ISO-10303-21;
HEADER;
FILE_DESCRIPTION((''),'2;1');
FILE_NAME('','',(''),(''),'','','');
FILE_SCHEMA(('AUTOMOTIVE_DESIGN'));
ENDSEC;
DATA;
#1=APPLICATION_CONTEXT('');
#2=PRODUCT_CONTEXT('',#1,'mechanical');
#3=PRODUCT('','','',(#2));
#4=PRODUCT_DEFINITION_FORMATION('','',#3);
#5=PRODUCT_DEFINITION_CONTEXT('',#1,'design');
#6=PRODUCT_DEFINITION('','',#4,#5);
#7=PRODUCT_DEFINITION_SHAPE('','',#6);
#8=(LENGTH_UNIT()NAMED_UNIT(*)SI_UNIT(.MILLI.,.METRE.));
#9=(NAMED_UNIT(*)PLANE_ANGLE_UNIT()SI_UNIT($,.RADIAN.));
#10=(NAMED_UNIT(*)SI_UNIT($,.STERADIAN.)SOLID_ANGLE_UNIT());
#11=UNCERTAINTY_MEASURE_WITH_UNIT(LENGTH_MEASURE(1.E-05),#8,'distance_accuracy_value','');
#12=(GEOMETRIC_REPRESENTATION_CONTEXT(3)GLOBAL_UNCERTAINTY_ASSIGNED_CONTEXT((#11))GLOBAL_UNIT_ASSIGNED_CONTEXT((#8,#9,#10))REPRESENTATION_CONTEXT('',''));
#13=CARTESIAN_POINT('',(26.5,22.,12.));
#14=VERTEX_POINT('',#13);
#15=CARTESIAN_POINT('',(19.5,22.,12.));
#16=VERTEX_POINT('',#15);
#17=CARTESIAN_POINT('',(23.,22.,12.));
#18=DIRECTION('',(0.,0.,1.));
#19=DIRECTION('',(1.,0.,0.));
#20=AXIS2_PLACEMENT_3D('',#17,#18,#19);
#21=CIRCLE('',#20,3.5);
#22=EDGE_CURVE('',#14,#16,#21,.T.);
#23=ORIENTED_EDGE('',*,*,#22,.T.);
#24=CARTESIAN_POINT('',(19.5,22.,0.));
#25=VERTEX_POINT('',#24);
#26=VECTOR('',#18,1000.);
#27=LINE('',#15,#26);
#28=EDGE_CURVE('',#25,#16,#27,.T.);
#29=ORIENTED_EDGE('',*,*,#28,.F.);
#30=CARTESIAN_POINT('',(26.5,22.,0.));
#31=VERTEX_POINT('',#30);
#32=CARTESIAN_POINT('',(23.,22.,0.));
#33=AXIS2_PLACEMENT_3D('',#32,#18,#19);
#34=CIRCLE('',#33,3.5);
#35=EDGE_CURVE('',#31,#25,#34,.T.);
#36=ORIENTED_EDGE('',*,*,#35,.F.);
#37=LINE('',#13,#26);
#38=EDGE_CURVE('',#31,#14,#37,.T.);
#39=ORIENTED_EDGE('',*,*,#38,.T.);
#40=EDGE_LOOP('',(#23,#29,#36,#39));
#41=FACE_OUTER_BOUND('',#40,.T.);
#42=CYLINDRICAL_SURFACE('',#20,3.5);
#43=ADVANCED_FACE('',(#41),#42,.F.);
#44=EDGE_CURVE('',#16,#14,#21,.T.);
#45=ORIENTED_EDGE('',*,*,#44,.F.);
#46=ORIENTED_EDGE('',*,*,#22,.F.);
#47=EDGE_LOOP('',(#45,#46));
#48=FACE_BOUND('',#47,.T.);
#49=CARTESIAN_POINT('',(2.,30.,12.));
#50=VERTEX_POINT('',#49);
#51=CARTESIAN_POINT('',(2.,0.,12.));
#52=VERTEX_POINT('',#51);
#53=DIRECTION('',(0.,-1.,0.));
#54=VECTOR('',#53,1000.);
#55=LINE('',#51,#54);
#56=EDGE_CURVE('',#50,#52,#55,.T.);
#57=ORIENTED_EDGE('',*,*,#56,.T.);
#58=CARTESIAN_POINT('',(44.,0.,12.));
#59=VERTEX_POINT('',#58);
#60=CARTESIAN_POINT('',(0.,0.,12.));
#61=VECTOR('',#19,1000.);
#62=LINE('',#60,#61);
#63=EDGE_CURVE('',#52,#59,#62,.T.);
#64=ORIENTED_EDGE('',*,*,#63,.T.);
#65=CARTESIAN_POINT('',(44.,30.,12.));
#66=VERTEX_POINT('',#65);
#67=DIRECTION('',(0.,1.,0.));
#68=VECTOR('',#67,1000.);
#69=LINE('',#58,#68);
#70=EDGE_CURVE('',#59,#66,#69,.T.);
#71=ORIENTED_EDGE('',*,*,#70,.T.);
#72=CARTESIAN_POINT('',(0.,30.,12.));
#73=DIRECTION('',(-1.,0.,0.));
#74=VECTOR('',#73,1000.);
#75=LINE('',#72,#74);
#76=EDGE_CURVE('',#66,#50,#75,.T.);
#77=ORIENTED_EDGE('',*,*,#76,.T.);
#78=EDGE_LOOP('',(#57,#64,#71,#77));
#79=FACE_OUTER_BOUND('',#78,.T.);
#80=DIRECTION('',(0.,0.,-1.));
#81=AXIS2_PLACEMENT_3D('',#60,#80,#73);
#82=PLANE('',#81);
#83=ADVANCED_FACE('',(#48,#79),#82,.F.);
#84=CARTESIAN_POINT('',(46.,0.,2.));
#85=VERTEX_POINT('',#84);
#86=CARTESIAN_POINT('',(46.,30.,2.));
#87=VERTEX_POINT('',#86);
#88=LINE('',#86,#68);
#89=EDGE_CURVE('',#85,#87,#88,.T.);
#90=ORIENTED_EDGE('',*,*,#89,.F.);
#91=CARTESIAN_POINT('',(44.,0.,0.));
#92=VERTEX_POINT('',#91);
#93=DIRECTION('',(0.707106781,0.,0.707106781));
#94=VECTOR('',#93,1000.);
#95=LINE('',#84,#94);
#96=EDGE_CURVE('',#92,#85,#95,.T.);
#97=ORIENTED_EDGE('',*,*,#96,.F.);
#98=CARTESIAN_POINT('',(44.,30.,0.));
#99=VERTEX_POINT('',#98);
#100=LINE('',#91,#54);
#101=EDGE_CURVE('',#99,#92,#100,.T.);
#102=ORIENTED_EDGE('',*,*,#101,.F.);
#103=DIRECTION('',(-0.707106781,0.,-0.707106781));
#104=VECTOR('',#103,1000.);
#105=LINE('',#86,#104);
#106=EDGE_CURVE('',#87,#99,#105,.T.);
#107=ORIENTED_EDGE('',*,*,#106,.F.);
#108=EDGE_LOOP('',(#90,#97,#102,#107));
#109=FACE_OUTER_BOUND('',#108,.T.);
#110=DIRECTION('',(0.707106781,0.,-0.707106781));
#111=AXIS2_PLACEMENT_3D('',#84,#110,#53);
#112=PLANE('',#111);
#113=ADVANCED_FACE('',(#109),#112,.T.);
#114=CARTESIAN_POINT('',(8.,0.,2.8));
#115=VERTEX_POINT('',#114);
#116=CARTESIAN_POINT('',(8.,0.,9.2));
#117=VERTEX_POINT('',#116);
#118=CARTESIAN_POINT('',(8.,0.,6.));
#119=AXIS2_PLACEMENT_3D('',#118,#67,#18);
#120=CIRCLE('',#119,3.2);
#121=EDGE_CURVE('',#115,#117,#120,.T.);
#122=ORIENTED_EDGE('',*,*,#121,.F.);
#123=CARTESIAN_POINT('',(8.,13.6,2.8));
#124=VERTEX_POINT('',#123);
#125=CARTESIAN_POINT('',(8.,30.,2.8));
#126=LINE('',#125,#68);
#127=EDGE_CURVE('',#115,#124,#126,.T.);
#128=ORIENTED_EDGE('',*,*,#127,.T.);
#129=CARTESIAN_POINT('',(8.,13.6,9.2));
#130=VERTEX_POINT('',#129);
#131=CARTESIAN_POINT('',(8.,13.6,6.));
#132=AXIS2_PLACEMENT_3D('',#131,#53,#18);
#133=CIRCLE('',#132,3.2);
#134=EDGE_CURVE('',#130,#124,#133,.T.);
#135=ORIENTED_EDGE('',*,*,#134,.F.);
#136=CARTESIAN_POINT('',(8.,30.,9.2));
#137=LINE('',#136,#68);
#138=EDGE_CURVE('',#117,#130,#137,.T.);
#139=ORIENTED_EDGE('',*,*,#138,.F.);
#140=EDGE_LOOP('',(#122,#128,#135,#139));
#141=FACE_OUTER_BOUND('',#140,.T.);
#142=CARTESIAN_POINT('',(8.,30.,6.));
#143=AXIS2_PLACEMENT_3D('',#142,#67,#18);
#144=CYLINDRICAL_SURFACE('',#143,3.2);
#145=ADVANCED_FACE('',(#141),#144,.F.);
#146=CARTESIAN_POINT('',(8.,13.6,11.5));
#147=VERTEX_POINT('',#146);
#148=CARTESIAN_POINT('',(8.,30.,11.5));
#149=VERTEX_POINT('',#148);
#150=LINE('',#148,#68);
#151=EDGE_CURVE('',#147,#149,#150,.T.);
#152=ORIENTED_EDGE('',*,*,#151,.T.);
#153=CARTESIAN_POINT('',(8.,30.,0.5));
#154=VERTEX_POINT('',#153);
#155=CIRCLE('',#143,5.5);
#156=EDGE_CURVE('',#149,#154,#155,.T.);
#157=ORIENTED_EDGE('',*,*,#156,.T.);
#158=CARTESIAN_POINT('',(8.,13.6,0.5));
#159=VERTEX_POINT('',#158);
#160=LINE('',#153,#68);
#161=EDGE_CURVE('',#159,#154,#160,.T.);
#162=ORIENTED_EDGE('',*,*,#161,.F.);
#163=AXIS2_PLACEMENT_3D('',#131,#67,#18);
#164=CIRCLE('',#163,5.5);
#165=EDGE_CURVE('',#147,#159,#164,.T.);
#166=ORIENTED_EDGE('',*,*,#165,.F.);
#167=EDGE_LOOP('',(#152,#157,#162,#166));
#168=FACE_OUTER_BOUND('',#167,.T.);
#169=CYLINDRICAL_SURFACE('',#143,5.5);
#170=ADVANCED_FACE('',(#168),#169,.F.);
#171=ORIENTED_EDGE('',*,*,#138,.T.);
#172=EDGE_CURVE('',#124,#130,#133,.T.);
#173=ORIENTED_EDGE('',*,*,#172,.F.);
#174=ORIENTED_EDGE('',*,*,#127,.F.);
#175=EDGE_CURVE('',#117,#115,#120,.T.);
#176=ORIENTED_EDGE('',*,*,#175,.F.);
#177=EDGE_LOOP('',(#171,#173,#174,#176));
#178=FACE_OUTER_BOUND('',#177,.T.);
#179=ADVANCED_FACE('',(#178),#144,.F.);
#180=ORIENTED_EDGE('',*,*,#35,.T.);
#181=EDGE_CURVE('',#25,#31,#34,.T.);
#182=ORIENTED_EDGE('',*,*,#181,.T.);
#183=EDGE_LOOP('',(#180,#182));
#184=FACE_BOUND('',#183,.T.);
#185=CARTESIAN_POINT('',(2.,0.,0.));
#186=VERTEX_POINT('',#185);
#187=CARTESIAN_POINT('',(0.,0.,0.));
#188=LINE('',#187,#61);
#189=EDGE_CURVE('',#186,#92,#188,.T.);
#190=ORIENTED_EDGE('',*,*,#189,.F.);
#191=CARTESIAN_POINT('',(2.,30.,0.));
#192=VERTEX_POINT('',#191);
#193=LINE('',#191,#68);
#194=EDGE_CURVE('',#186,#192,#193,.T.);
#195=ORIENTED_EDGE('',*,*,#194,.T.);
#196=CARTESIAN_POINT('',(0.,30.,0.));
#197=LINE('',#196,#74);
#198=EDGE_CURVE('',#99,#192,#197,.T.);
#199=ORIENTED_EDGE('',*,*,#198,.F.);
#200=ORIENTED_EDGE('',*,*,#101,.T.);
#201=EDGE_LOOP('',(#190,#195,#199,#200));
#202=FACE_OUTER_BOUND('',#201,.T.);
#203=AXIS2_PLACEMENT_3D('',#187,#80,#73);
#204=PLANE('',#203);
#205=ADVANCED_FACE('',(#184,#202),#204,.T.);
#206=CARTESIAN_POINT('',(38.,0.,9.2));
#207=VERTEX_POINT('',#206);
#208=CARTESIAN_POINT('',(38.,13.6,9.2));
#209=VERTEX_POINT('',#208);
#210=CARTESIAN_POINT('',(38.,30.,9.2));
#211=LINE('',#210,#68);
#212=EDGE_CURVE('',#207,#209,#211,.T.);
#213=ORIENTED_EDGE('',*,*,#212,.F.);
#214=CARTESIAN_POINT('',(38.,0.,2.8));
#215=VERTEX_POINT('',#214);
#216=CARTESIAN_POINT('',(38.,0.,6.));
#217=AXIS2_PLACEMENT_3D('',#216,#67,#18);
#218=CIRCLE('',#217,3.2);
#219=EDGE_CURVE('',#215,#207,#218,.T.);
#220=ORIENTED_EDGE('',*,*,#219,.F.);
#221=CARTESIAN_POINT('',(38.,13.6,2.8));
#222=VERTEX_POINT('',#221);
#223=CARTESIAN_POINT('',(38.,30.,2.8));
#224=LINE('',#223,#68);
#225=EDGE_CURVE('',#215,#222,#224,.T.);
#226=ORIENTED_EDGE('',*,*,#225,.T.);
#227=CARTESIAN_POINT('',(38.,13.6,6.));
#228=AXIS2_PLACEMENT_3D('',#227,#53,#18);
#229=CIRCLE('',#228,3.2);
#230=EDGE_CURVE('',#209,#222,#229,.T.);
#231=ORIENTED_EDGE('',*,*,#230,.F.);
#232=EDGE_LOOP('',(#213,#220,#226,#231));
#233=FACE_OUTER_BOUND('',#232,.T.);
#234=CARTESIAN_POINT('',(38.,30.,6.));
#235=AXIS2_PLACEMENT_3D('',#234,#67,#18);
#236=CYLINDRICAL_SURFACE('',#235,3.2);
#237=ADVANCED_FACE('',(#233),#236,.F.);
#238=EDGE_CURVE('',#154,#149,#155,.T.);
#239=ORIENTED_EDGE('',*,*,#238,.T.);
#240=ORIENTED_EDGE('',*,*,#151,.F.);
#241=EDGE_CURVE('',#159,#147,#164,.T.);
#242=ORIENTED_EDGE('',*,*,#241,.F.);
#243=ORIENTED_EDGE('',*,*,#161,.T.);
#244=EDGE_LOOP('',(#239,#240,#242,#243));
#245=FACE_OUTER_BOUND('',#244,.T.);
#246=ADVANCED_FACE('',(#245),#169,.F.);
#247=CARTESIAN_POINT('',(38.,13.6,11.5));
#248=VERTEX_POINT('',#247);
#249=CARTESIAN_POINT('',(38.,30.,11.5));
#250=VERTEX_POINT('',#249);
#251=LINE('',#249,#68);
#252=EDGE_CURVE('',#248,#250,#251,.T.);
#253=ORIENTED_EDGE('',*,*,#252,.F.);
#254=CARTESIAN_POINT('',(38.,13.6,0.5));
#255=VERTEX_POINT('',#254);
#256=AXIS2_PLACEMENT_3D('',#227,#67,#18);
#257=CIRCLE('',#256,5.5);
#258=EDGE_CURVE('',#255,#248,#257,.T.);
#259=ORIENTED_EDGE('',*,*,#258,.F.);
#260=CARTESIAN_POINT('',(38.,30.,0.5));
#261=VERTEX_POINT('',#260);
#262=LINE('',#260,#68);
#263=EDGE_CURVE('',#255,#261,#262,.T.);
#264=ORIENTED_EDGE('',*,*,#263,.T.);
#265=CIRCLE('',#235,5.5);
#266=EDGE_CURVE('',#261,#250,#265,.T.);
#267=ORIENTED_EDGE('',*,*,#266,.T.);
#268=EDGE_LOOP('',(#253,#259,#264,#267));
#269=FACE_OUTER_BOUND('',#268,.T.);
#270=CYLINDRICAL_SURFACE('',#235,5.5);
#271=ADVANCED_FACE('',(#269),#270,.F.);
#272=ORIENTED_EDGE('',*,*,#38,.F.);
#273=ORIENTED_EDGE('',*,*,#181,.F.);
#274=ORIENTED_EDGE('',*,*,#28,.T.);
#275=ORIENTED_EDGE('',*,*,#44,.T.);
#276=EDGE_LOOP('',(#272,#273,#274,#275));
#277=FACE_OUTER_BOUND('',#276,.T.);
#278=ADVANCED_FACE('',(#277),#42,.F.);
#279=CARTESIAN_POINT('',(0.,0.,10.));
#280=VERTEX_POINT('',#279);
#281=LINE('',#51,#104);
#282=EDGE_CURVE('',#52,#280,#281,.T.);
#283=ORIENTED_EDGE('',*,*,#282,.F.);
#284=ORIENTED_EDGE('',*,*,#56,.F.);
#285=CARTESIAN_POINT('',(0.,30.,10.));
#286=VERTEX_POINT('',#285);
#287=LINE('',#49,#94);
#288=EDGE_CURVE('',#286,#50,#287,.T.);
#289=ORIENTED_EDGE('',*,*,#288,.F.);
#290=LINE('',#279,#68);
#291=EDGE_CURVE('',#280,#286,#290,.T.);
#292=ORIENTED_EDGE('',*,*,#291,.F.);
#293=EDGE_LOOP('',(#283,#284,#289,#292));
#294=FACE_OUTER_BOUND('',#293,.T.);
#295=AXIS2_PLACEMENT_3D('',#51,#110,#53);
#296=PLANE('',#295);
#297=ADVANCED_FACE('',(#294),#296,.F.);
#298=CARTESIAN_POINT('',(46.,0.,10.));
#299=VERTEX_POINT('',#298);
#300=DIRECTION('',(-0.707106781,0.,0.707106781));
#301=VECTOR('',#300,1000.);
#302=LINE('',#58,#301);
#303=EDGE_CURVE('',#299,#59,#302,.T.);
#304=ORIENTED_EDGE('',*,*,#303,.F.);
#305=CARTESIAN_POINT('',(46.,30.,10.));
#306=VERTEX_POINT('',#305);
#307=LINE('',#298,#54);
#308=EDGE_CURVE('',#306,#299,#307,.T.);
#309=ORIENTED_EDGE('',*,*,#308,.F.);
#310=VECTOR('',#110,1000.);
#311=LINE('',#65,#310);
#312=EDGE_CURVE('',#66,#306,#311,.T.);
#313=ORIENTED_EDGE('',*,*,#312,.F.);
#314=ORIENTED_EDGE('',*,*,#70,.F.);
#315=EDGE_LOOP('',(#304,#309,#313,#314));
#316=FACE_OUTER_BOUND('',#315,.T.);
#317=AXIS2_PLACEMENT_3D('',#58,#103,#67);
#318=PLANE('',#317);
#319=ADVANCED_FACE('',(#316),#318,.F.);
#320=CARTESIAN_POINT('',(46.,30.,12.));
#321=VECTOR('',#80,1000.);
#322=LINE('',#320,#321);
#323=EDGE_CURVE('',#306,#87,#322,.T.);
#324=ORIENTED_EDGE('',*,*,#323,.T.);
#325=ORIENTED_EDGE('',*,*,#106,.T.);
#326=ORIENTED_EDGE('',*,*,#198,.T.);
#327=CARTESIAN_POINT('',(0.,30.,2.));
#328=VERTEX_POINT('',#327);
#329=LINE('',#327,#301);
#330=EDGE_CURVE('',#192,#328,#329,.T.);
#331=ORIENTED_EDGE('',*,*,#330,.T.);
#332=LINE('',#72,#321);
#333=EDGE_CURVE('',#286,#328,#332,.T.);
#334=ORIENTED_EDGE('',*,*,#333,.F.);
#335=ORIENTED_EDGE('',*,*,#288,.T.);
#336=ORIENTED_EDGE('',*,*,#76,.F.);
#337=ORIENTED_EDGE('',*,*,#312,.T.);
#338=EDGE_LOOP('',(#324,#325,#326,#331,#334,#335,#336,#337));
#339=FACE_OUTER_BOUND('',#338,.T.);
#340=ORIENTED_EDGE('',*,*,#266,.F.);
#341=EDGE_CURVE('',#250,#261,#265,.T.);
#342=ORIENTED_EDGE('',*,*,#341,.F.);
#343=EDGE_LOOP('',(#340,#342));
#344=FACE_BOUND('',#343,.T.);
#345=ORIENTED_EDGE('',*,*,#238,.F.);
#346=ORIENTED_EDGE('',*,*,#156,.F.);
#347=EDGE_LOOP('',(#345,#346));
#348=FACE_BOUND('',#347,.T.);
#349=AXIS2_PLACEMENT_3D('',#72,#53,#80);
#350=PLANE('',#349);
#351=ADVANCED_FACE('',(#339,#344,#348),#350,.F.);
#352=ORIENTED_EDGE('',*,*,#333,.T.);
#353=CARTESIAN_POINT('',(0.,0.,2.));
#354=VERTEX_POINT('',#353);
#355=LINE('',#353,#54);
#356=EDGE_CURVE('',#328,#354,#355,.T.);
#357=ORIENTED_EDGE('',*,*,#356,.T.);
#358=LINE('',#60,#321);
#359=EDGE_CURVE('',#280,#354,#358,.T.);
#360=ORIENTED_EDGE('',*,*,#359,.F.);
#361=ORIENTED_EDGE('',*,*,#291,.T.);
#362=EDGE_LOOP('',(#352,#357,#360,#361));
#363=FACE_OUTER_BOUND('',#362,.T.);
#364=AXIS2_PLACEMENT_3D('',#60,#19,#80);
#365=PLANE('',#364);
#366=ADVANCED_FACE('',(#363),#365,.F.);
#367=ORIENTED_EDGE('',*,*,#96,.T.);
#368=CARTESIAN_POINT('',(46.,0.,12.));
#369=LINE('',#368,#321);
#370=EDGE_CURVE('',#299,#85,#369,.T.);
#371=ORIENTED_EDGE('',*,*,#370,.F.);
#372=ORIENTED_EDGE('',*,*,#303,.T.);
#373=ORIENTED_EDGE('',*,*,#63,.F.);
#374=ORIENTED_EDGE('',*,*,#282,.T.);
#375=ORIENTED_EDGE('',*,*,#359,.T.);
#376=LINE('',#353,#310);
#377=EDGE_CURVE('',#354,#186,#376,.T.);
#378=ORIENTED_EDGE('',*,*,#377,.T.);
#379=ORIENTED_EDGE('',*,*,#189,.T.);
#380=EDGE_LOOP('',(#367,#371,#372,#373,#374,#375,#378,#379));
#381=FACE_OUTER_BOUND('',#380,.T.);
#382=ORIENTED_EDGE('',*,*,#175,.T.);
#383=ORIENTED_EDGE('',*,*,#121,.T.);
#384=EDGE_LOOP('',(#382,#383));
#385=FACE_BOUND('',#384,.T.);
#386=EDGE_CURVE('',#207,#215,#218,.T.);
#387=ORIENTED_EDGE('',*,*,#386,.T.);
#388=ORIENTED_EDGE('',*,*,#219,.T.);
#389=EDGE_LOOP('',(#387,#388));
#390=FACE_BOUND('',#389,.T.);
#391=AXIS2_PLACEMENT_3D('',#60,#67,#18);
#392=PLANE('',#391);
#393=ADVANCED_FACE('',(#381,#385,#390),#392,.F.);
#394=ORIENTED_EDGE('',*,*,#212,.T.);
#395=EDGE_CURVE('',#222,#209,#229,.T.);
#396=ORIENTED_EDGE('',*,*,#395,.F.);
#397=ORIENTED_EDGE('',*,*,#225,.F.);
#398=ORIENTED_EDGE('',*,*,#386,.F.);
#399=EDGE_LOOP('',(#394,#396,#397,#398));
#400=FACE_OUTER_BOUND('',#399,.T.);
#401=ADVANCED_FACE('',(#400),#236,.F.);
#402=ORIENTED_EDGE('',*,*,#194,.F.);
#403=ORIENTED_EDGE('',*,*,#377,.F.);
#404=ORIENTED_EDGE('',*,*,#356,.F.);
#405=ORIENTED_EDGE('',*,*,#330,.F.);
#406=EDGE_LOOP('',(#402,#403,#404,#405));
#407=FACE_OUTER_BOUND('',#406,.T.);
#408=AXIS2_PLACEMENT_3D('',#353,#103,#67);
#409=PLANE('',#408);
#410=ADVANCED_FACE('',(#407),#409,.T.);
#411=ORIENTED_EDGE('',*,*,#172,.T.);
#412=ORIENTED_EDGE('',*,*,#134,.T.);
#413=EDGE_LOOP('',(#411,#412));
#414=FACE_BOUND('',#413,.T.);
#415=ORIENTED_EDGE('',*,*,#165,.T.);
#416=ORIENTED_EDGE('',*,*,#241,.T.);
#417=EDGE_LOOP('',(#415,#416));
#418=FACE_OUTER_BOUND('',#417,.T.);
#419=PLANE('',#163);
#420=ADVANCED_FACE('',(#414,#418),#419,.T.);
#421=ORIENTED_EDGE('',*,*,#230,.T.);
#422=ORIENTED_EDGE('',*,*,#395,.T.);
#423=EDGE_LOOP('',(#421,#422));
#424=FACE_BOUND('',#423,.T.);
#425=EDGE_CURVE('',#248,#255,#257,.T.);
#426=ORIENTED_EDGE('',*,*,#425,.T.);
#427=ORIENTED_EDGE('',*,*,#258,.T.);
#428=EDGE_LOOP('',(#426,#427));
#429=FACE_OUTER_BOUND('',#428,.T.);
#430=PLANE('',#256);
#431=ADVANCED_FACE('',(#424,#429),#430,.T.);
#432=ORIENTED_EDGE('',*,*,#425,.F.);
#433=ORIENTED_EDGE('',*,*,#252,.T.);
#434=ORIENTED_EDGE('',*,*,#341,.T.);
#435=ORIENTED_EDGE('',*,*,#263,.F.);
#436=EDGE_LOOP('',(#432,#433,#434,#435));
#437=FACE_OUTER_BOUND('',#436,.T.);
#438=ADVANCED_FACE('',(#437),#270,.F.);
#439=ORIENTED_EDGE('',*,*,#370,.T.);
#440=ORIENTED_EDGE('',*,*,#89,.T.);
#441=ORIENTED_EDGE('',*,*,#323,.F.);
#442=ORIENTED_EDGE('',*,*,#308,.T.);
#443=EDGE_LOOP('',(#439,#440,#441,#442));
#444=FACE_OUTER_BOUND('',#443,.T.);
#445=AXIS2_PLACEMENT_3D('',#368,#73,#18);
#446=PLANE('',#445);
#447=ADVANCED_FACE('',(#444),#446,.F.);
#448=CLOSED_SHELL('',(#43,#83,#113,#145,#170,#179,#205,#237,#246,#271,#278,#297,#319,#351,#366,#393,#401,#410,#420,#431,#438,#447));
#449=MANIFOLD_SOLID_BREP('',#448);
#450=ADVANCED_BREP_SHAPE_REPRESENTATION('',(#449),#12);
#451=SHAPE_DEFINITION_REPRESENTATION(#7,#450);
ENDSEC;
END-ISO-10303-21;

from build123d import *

# Parameters (mm, degrees)
SKETCH_1_W                   = 46
SKETCH_1_H                   = 30
EXTRUDE_1_DEPTH              = 12
HOLE_WIZARD_7_0_7_1_D        = 7
HOLE_WIZARD_M6_1_D           = 6.4
HOLE_WIZARD_M6_1_CBORE_D     = 11
HOLE_WIZARD_M6_1_CBORE_DEPTH = 6.4
SKETCH_7_R                   = 5.5
CUT_EXTRUDE_1_DEPTH          = 10
CHAMFER_1_SIZE               = 2


with BuildPart() as part:
    # 草图1 → 凸台-拉伸1 (new body)
    with BuildSketch(Plane.XY):
        with Locations((23, 15)):
            Rectangle(SKETCH_1_W, SKETCH_1_H)
    extrude(amount=EXTRUDE_1_DEPTH)

    # Ø7.0 (7) 直径孔1 (through all)
    with Locations(Plane.XY.offset(12)):
        with Locations((23, 22)):
            Hole(HOLE_WIZARD_7_0_7_1_D / 2)

    # M6 六角凹头螺钉的柱形沉头孔1 (through all)
    with Locations(Plane(origin=(0, 30, 0), x_dir=(1, 0, 0), z_dir=(0, 1, 0))):
        with Locations((8, -6), (38, -6)):
            CounterBoreHole(HOLE_WIZARD_M6_1_D / 2, HOLE_WIZARD_M6_1_CBORE_D / 2, HOLE_WIZARD_M6_1_CBORE_DEPTH)

    # 草图7 → 切除-拉伸1 (cut)
    with BuildSketch(Plane(origin=(0, 23.6, 0), x_dir=(1, 0, 0), z_dir=(0, 1, 0))):
        with Locations(Location((8, -6, 0), (0, 0, 270))):
            Circle(SKETCH_7_R)
        with Locations(Location((38, -6, 0), (0, 0, 270))):
            Circle(SKETCH_7_R)
    extrude(amount=-CUT_EXTRUDE_1_DEPTH, mode=Mode.SUBTRACT)

    # 倒角1
    chamfer_1_edges = [part.edges().sort_by_distance(p)[0] for p in [
        (46, 15, 12),
        (0, 15, 12),
        (46, 15, 0),
        (0, 15, 0),
    ]]
    chamfer(chamfer_1_edges, length=CHAMFER_1_SIZE)


solid = part.part
